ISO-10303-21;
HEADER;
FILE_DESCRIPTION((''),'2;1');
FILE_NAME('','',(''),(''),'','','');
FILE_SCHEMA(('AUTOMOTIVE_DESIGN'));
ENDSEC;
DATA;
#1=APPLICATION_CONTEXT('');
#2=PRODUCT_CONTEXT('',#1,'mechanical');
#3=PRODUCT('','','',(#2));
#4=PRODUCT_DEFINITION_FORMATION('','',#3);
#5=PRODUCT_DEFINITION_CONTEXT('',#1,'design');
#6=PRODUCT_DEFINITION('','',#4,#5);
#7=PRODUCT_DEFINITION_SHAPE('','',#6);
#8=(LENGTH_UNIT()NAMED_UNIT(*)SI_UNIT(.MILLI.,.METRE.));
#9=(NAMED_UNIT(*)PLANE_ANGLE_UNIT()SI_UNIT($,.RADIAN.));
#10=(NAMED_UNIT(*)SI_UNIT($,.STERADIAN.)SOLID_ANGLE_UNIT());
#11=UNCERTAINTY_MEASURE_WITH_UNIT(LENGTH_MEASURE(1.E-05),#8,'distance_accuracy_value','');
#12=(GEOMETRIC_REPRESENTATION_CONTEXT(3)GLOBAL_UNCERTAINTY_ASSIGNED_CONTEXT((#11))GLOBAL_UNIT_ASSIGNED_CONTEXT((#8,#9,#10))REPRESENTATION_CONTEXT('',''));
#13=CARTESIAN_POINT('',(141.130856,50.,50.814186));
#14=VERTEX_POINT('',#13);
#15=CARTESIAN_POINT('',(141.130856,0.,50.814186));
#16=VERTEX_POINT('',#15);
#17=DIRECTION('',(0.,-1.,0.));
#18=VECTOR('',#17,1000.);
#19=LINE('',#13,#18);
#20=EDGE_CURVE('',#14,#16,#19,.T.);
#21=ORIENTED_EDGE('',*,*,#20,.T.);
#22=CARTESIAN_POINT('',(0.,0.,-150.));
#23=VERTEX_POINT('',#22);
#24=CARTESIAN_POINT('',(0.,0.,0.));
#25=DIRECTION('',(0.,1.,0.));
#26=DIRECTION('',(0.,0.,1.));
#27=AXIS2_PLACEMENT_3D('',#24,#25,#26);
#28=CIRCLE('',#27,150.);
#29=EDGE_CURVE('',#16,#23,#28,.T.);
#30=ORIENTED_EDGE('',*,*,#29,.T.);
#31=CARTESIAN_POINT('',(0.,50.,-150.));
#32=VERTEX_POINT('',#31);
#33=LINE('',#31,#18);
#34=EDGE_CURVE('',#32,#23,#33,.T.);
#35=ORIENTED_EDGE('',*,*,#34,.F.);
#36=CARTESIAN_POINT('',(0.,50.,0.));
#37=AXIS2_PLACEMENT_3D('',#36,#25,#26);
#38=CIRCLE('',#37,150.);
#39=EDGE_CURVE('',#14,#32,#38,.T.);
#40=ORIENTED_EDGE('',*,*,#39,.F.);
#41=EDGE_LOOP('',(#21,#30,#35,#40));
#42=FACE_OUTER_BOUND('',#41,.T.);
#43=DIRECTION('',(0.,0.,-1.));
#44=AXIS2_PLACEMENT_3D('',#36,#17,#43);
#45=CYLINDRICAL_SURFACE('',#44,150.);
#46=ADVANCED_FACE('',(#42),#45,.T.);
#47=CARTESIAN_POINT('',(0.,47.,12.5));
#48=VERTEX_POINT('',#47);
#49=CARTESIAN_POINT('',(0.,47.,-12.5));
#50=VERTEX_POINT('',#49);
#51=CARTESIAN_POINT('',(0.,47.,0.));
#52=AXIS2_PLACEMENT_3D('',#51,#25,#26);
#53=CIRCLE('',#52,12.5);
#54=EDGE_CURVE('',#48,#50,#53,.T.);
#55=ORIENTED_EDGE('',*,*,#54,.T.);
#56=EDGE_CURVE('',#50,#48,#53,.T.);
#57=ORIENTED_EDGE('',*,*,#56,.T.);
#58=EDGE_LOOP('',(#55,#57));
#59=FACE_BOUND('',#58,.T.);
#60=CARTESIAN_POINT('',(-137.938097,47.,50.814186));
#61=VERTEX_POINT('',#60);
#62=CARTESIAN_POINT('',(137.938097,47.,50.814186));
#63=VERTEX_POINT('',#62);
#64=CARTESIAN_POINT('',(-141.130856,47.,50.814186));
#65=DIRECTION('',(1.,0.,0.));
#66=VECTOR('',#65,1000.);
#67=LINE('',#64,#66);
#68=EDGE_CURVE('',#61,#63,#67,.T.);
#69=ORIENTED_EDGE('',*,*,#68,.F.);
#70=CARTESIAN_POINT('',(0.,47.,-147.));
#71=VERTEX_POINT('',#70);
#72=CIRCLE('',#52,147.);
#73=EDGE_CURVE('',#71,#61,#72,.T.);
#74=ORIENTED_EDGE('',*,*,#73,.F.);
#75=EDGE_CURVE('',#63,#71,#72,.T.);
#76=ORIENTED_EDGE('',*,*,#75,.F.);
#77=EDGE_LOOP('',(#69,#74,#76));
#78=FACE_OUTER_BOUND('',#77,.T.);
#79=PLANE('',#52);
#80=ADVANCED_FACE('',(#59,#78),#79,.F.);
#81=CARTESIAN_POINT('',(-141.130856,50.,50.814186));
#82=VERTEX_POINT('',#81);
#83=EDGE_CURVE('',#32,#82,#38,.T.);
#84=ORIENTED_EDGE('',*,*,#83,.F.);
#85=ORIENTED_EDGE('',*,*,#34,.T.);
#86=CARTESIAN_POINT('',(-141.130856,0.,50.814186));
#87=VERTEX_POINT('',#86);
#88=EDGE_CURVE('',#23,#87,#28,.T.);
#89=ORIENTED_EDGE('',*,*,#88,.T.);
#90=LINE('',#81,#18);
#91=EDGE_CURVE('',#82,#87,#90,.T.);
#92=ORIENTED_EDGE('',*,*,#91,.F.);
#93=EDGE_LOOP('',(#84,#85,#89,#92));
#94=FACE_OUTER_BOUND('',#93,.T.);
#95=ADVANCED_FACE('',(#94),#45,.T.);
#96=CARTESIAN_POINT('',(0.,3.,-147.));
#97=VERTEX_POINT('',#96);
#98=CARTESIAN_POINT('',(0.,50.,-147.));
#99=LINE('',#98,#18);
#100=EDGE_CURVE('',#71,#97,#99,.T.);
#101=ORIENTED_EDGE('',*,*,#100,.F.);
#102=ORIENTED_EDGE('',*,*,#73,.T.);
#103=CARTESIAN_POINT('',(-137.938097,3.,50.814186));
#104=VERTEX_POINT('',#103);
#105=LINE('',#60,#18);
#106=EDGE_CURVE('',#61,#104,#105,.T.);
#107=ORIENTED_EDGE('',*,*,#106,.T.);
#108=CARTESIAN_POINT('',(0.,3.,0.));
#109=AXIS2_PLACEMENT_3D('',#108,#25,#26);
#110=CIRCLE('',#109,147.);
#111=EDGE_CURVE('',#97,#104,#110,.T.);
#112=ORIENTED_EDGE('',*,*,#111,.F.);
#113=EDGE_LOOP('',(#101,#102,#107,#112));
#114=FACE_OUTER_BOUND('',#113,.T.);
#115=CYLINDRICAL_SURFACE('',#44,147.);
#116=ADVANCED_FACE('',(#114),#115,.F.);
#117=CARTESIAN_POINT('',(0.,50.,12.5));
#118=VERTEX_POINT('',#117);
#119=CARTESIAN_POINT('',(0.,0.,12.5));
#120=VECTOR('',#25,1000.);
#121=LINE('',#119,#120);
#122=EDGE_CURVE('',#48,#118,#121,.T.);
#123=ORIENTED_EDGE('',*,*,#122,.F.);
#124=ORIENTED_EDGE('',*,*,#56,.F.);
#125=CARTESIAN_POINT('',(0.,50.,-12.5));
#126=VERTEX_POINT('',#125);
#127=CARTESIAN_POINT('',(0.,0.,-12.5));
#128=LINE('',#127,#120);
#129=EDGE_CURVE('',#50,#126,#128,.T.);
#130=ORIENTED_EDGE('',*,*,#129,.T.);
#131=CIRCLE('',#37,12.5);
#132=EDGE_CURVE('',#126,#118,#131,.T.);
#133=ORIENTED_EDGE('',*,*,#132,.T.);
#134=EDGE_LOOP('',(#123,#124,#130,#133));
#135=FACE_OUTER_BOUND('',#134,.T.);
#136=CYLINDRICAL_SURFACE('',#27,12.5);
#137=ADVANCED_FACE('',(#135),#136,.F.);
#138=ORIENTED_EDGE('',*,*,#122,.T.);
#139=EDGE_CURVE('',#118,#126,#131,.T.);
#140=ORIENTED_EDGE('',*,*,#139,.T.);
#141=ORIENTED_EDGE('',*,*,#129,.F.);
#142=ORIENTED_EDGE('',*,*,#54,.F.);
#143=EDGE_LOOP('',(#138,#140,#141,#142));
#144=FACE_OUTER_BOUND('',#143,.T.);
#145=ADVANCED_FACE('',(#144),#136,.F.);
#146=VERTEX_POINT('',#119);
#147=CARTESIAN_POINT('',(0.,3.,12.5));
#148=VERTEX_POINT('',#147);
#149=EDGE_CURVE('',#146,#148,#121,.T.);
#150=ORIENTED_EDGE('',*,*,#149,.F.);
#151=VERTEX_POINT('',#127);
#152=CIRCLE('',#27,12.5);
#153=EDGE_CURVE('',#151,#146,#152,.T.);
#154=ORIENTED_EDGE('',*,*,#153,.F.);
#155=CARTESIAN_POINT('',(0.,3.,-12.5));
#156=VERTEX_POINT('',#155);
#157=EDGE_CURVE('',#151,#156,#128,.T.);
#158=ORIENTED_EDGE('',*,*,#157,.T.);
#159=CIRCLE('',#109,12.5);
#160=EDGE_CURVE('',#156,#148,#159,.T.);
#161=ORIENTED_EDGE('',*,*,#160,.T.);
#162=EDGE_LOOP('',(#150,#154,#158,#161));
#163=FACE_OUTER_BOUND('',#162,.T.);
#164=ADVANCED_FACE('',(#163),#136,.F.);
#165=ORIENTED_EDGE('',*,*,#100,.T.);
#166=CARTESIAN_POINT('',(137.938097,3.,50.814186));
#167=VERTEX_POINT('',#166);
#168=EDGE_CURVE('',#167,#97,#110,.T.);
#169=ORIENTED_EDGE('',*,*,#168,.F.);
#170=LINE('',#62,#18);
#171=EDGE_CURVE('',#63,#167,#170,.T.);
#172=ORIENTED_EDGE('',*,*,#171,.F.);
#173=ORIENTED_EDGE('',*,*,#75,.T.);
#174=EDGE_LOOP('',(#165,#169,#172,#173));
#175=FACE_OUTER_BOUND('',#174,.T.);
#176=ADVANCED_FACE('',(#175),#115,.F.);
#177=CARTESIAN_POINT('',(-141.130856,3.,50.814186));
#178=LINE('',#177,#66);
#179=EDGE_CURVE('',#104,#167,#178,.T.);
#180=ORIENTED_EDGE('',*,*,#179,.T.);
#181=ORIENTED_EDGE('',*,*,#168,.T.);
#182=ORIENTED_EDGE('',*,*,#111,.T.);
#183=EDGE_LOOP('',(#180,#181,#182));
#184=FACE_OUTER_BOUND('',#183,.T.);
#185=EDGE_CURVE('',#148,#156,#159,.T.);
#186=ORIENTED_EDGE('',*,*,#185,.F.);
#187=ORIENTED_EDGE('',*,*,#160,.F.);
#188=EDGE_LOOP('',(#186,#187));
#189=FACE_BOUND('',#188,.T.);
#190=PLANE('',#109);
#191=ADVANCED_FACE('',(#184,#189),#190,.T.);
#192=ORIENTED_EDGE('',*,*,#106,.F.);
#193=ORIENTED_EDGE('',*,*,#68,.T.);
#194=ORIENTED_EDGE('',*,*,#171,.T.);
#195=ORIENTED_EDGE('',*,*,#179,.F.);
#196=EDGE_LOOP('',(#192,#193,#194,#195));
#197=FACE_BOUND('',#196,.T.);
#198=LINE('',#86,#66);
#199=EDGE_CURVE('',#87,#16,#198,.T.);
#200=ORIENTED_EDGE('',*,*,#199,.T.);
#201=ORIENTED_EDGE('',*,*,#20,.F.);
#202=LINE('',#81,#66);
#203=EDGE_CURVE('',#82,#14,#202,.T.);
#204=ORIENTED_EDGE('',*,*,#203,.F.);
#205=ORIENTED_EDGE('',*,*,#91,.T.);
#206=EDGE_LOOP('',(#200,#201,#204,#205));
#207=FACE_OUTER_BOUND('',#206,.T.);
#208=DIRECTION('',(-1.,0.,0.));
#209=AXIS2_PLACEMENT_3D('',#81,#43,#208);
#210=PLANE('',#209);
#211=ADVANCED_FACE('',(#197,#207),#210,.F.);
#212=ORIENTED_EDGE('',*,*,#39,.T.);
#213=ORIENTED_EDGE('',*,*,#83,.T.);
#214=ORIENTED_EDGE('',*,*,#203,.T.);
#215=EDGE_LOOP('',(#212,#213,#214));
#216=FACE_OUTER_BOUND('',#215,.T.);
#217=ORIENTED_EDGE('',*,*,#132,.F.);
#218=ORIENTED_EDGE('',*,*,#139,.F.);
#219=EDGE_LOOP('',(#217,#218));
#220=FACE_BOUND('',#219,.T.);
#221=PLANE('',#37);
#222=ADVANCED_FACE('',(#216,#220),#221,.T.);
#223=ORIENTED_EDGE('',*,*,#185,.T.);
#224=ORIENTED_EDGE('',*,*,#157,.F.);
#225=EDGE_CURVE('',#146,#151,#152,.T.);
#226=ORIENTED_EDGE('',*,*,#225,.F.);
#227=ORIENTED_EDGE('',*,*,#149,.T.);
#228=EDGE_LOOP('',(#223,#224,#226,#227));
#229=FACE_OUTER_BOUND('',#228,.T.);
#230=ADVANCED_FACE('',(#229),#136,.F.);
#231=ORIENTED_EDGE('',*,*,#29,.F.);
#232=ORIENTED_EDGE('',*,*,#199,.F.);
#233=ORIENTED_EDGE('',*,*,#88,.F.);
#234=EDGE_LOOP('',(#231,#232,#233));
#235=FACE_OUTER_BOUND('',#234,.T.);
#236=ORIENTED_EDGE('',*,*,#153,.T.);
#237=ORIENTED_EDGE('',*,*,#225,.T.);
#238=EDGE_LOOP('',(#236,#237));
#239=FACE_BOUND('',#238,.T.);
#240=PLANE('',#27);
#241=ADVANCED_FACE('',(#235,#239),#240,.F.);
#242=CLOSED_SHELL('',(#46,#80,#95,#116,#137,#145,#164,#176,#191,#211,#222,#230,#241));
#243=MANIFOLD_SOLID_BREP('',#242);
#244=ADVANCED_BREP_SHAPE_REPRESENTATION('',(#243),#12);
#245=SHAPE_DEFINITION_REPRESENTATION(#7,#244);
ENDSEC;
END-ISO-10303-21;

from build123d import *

# Parameters (mm, degrees)
BOSS_EXTRUDE1_DEPTH     = 50
SHELL1_T                = -3
CUT_EXTRUDE1_DEPTH      = 218.944947177
CUT_EXTRUDE1_DEPTH_BACK = 218.944947177
SKETCH2_R               = 12.5


with BuildPart() as part:
    # Sketch1 → Boss-Extrude1 (new body)
    with BuildSketch(Plane(origin=(0, 0, 0), x_dir=(1, 0, 0), z_dir=(0, 1, 0))):
        with BuildLine():
            Line((-141.13085598, -50.814185916), (141.13085598, -50.814185916))
            ThreePointArc((141.13085598, -50.814185916), (0, 150), (-141.13085598, -50.814185916))
        make_face()
    extrude(amount=BOSS_EXTRUDE1_DEPTH)

    # Shell1
    shell1_openings = [part.faces().sort_by_distance(p)[0] for p in [
        (0, 25, 50.814185916),
    ]]
    offset(amount=SHELL1_T, openings=shell1_openings)

    # Sketch2 → Cut-Extrude1 (cut, two sides: drawn at the far end of the back side and taken through both)
    with BuildSketch(Plane(origin=(0, 50, 0), x_dir=(1, 0, 0), z_dir=(0, 1, 0)).offset(-CUT_EXTRUDE1_DEPTH_BACK)):
        with Locations(Location((0, 0, 0), (0, 0, 270))):
            Circle(SKETCH2_R)
    extrude(amount=CUT_EXTRUDE1_DEPTH + CUT_EXTRUDE1_DEPTH_BACK, mode=Mode.SUBTRACT)


solid = part.part
